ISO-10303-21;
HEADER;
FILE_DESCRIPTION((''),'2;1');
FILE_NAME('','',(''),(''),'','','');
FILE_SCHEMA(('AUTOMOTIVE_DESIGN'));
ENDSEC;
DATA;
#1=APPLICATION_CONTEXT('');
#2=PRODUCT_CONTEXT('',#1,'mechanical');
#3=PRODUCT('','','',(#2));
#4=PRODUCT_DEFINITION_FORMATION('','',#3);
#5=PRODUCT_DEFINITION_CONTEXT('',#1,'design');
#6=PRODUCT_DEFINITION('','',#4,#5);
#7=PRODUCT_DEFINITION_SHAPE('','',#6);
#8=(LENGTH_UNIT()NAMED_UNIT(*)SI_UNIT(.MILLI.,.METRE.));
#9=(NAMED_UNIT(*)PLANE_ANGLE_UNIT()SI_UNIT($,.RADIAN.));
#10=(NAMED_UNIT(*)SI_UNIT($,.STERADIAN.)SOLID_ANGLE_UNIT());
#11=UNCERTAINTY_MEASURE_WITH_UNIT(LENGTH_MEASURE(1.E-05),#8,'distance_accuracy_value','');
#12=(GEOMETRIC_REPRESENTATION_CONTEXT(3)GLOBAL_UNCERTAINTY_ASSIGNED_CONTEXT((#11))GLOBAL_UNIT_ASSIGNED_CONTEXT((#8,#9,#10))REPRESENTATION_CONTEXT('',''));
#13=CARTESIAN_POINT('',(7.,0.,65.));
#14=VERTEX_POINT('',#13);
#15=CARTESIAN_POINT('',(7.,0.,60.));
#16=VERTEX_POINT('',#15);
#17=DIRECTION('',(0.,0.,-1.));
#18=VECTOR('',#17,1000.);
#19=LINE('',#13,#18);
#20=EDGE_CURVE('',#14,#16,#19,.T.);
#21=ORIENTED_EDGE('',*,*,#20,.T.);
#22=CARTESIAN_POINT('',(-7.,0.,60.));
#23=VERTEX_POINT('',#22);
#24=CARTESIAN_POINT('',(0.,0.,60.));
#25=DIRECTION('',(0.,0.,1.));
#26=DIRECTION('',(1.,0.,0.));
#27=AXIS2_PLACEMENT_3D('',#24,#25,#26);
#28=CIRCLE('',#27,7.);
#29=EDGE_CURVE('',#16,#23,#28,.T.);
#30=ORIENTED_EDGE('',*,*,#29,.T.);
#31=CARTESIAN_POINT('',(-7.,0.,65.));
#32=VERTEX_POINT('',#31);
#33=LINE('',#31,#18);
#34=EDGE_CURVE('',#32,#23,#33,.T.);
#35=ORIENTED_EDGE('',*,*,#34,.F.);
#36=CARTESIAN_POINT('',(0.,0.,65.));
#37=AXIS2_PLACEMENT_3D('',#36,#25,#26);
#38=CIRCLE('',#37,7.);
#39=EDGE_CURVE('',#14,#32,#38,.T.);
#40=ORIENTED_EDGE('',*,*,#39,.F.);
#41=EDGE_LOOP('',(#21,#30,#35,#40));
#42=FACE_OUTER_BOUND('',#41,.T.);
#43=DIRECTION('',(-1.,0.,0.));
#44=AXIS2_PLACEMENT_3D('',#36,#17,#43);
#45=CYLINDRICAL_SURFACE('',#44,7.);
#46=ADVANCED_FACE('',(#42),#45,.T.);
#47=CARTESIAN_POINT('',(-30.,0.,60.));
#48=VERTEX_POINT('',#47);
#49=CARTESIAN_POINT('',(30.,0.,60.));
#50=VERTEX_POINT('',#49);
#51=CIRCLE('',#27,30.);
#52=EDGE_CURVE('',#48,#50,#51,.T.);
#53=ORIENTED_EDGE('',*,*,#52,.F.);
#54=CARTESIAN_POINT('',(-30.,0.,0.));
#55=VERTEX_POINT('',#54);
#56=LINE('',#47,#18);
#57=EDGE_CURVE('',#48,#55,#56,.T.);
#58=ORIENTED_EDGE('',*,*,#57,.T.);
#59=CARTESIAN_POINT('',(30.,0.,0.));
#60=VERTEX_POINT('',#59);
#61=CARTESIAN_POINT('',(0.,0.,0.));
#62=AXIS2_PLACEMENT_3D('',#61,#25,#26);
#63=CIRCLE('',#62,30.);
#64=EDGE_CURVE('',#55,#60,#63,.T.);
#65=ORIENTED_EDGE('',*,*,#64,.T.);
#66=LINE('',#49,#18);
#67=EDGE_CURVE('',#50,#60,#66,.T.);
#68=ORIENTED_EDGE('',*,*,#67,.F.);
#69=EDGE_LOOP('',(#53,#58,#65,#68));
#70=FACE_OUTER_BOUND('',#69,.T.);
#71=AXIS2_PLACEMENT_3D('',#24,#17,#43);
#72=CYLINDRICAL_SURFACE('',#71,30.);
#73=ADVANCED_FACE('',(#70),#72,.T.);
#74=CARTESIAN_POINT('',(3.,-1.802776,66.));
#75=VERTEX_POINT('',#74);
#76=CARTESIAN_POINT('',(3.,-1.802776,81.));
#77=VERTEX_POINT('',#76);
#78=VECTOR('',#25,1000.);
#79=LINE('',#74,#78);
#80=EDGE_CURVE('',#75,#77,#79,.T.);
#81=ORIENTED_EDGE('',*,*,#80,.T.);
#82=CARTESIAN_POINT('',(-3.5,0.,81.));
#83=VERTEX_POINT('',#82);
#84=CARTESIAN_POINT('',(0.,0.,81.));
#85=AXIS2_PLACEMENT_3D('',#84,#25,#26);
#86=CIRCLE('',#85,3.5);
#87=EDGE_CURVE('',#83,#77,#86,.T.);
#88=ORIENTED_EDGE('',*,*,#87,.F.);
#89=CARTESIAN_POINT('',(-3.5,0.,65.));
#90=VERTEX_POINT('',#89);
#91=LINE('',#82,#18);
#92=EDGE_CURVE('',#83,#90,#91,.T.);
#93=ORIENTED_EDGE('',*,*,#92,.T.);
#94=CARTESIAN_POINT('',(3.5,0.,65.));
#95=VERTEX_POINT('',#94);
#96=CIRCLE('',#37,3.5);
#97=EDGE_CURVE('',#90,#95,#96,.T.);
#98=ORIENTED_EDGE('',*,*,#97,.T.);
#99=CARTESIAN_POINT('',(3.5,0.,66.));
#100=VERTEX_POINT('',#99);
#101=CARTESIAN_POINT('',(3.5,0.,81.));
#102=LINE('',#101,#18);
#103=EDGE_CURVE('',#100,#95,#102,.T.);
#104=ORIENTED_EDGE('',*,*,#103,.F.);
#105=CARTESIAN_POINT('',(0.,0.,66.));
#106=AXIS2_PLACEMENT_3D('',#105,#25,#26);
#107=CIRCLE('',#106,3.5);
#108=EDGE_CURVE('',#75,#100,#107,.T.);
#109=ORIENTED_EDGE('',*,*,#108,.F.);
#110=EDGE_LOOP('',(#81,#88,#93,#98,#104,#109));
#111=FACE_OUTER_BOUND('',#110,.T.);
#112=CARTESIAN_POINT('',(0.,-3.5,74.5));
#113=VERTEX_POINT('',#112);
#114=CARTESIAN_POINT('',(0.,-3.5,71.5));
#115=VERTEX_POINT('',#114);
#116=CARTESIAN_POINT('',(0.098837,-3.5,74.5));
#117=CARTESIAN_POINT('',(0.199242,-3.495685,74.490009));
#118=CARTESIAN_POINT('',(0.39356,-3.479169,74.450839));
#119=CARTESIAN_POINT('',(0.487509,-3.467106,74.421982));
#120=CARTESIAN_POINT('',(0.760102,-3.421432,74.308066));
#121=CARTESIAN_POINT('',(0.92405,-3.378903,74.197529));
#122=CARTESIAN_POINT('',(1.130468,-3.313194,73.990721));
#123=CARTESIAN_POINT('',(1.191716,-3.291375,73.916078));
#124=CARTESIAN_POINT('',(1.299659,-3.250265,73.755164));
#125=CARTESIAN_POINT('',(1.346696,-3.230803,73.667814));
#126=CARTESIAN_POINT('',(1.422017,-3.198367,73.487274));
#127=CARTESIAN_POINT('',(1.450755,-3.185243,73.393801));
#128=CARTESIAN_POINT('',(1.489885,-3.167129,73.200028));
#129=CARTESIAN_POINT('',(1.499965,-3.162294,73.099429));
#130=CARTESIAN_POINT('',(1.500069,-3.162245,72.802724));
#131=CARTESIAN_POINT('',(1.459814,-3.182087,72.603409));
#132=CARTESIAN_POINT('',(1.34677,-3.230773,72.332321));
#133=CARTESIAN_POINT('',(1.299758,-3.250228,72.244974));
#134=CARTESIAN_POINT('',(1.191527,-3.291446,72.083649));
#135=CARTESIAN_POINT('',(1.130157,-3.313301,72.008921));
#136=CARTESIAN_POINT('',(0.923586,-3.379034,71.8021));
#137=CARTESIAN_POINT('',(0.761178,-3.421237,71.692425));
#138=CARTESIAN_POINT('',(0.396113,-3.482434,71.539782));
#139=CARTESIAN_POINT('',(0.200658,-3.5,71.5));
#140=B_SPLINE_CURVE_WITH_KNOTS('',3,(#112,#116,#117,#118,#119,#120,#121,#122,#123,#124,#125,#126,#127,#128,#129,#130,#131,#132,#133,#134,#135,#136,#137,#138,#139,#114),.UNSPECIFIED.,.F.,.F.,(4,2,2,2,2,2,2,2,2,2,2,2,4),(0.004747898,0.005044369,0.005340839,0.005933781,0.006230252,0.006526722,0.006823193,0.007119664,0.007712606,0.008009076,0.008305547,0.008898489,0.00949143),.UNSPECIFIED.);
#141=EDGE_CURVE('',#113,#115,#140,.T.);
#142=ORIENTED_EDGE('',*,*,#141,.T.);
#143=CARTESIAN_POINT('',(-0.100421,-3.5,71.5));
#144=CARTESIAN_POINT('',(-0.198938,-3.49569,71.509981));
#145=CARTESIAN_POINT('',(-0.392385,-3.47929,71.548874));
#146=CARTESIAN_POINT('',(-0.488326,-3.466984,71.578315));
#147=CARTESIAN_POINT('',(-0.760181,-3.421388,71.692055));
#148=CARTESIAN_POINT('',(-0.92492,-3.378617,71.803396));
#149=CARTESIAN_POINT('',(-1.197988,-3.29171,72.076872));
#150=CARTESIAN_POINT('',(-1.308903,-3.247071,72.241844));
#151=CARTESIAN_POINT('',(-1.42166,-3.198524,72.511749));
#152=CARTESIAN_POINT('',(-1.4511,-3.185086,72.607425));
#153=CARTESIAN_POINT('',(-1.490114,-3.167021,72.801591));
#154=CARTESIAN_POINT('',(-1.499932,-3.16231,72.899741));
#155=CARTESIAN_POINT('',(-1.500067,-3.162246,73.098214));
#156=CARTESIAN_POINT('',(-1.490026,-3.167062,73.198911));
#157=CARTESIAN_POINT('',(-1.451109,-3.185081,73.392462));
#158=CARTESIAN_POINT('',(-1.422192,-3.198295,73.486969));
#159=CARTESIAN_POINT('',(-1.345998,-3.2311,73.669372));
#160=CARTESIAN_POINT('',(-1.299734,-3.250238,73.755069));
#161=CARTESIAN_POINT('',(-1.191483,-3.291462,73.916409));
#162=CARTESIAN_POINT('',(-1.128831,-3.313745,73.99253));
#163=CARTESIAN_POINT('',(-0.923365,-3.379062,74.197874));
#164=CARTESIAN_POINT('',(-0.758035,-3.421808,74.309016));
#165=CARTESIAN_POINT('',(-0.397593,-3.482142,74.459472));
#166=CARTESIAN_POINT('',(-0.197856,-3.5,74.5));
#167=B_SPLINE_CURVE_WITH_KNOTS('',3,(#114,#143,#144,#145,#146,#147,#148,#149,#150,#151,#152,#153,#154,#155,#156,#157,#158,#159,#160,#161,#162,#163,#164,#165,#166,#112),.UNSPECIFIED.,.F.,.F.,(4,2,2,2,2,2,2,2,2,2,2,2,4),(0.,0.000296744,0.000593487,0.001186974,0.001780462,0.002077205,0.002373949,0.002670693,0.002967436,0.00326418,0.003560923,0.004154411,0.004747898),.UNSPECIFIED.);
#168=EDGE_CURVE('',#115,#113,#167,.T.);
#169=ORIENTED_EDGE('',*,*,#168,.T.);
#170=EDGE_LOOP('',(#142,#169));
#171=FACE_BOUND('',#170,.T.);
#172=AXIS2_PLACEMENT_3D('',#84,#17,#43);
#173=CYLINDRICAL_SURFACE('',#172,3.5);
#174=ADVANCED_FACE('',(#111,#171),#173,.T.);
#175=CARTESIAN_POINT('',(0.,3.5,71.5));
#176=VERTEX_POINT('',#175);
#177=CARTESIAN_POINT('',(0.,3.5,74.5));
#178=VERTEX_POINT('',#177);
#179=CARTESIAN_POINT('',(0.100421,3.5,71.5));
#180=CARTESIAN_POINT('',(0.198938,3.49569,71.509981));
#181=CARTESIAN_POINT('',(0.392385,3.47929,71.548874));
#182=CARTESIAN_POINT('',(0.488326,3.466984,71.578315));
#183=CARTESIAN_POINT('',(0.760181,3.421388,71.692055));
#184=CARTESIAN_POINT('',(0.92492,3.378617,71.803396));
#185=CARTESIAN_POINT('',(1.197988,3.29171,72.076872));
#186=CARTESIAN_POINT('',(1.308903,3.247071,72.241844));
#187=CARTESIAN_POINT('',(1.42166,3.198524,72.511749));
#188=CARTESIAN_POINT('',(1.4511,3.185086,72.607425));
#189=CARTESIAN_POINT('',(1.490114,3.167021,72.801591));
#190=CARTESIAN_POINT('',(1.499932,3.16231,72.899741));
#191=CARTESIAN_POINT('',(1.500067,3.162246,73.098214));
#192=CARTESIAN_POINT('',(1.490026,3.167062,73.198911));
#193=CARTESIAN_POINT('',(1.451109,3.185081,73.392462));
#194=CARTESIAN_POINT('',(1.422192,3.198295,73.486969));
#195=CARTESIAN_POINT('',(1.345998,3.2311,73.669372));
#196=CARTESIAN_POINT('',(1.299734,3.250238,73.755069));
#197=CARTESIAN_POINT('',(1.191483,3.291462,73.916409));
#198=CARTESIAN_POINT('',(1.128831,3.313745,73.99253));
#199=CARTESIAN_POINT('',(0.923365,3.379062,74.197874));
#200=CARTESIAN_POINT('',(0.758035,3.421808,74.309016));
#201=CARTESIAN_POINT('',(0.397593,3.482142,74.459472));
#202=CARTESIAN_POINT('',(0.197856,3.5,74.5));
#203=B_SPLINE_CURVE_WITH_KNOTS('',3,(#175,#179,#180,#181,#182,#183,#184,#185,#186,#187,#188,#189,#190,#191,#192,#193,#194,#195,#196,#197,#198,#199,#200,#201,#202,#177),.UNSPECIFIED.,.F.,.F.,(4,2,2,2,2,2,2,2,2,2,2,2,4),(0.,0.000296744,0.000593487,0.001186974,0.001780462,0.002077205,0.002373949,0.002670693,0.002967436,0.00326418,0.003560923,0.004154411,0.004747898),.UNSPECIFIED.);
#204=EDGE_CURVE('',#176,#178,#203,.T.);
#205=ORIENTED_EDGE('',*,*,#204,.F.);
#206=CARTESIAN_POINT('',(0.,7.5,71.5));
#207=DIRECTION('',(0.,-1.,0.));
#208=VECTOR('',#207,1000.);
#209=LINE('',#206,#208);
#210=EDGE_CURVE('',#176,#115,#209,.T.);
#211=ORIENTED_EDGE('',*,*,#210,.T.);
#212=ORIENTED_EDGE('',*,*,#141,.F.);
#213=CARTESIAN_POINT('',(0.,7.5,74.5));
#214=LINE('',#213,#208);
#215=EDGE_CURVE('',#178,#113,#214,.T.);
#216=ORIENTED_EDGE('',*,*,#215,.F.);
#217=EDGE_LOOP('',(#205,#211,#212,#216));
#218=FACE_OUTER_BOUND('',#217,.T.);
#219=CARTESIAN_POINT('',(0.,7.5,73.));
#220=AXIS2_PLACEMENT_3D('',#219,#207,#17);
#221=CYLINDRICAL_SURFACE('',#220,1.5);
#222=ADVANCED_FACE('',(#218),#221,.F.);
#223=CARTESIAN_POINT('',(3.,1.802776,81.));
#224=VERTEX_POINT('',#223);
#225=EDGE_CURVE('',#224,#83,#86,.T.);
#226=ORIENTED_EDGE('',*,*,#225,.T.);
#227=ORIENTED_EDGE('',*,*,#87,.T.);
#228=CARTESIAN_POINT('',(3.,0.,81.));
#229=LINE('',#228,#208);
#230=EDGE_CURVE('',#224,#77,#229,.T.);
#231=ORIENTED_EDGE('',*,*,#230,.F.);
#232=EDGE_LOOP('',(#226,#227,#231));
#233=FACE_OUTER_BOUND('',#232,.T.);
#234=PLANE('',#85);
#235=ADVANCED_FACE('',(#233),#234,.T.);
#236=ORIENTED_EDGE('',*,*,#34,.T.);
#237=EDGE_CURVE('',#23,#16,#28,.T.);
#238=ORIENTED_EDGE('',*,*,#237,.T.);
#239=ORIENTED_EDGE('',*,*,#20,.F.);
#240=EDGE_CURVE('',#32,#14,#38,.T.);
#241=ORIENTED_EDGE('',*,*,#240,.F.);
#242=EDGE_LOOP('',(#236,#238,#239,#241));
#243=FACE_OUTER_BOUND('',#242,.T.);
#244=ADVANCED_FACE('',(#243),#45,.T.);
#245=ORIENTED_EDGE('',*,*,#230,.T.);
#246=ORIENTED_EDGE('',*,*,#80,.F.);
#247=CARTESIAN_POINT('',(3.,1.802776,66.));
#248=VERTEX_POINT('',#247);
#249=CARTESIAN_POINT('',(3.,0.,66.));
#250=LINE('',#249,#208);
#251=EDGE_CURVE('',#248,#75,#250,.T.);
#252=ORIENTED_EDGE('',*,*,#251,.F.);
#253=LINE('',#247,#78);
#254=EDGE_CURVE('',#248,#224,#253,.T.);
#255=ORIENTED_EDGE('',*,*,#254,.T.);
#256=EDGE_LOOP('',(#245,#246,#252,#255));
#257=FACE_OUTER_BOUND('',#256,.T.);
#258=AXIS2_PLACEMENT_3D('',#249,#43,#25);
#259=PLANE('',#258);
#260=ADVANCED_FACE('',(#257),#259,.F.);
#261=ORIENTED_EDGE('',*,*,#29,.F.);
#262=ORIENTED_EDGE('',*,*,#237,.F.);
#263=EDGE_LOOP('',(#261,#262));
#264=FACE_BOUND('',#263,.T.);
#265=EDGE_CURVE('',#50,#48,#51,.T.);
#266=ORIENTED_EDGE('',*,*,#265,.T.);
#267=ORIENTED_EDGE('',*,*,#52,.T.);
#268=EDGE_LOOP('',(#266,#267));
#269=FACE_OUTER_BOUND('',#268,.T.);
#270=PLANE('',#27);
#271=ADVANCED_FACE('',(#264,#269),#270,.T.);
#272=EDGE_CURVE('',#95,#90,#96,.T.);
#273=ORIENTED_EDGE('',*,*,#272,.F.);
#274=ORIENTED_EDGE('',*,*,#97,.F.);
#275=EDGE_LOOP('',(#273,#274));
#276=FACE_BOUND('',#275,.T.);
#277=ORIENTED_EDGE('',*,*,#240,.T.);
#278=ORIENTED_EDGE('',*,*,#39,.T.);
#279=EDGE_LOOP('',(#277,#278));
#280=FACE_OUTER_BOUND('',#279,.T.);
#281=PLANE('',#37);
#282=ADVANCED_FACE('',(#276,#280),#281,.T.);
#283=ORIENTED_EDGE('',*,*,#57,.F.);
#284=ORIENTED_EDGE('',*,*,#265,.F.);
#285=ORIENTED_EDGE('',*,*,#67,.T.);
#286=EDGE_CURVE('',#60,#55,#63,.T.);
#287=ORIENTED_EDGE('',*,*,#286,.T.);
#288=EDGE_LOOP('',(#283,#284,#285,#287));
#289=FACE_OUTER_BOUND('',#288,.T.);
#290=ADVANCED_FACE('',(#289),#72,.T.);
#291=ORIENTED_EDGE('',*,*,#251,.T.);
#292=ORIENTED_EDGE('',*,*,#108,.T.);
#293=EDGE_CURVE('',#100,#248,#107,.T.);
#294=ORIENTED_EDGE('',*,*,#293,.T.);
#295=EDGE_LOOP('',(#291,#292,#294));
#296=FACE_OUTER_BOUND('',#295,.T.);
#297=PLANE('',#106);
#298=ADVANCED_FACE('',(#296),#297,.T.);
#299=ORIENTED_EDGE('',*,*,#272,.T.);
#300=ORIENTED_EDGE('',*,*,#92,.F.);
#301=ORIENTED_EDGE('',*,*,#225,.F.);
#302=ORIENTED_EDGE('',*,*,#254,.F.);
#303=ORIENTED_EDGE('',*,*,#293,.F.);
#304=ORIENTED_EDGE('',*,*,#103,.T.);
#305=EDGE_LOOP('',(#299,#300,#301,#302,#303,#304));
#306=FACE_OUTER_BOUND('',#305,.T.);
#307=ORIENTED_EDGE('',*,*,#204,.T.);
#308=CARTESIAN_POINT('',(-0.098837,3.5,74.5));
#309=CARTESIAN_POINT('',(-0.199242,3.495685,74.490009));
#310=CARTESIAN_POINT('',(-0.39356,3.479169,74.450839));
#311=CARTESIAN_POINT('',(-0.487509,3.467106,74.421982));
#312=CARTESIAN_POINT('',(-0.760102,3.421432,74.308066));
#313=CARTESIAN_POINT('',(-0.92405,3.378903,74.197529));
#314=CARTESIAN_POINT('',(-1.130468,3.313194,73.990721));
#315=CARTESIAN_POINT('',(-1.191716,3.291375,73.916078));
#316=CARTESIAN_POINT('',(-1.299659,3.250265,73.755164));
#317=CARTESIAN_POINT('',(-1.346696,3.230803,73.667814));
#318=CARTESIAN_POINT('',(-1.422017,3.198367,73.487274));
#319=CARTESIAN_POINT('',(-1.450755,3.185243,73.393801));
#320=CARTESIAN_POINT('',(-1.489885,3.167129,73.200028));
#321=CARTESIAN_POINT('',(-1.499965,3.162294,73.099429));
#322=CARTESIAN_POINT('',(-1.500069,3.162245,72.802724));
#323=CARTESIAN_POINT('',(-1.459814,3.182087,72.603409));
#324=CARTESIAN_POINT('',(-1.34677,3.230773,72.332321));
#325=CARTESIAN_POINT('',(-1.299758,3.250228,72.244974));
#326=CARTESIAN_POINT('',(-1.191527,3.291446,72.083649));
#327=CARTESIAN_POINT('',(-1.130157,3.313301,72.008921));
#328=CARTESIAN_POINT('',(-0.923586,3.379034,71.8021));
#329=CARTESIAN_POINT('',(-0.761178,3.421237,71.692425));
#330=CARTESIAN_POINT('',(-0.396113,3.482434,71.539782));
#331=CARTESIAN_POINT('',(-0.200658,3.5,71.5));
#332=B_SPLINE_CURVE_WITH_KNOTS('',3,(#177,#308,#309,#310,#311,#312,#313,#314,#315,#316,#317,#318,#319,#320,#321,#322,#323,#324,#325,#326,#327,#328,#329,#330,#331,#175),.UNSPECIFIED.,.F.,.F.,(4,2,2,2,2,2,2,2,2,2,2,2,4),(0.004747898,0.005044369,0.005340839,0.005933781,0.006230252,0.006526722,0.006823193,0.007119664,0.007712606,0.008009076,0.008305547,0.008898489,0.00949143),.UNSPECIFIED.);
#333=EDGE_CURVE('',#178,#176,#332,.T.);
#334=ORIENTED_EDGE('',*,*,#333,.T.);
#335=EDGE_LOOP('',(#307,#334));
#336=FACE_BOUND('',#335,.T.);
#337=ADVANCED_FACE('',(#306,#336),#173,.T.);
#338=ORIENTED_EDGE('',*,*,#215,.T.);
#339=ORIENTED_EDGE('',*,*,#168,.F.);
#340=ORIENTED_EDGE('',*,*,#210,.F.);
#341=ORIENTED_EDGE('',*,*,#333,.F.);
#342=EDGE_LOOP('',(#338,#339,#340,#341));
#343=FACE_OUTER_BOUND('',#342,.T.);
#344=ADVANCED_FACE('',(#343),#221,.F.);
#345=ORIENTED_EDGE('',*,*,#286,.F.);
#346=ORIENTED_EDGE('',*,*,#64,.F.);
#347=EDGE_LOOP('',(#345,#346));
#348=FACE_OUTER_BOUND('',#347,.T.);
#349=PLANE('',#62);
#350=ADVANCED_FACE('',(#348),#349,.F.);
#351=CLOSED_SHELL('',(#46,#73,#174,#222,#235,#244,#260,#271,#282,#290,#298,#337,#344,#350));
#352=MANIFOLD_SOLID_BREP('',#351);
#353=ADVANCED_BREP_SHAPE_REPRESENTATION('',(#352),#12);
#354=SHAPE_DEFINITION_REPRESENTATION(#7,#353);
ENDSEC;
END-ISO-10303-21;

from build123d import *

# Parameters (mm, degrees)
SKETCH_1_R          = 30
EXTRUDE_1_DEPTH     = 60
SKETCH_2_R          = 7
EXTRUDE_2_DEPTH     = 5
SKETCH_3_R          = 3.5
EXTRUDE_3_DEPTH     = 16
CUT_EXTRUDE_START   = -15
CUT_EXTRUDE_1_DEPTH = 15
SKETCH_5_R          = 1.5
CUT_EXTRUDE_2_DEPTH = 7.5


with BuildPart() as part:
    # 草图1 → 凸台-拉伸1 (new body)
    with BuildSketch(Plane.XY):
        Circle(SKETCH_1_R)
    extrude(amount=EXTRUDE_1_DEPTH)

    # 草图2 → 凸台-拉伸2 (add)
    with BuildSketch(Plane.XY.offset(60)):
        Circle(SKETCH_2_R)
    extrude(amount=EXTRUDE_2_DEPTH)

    # 草图3 → 凸台-拉伸3 (add)
    with BuildSketch(Plane.XY.offset(65)):
        Circle(SKETCH_3_R)
    extrude(amount=EXTRUDE_3_DEPTH)

    # 草图4 → 切除-拉伸1 (cut)
    with BuildSketch(Plane.XY.offset(81).offset(CUT_EXTRUDE_START)):
        with BuildLine():
            ThreePointArc((3.5, 0), (3.372684391, 0.935414347), (3, 1.802775638))
            Line((3, 1.802775638), (3, 0))
            Line((3, 0), (3.5, 0))
        make_face()
        with BuildLine():
            Line((3.5, 0), (3, 0))
            Line((3, 0), (3, -1.802775638))
            ThreePointArc((3, -1.802775638), (3.372684391, -0.935414347), (3.5, 0))
        make_face()
    extrude(amount=CUT_EXTRUDE_1_DEPTH, mode=Mode.SUBTRACT)

    # 草图5 → 切除-拉伸2 (cut, symmetric)
    with BuildSketch(Plane(origin=(3, 0, 0), x_dir=(0, 0, -1), z_dir=(0, -1, 0))):
        with Locations((-73, -3)):
            Circle(SKETCH_5_R)
    extrude(amount=CUT_EXTRUDE_2_DEPTH, both=True, mode=Mode.SUBTRACT)


solid = part.part
